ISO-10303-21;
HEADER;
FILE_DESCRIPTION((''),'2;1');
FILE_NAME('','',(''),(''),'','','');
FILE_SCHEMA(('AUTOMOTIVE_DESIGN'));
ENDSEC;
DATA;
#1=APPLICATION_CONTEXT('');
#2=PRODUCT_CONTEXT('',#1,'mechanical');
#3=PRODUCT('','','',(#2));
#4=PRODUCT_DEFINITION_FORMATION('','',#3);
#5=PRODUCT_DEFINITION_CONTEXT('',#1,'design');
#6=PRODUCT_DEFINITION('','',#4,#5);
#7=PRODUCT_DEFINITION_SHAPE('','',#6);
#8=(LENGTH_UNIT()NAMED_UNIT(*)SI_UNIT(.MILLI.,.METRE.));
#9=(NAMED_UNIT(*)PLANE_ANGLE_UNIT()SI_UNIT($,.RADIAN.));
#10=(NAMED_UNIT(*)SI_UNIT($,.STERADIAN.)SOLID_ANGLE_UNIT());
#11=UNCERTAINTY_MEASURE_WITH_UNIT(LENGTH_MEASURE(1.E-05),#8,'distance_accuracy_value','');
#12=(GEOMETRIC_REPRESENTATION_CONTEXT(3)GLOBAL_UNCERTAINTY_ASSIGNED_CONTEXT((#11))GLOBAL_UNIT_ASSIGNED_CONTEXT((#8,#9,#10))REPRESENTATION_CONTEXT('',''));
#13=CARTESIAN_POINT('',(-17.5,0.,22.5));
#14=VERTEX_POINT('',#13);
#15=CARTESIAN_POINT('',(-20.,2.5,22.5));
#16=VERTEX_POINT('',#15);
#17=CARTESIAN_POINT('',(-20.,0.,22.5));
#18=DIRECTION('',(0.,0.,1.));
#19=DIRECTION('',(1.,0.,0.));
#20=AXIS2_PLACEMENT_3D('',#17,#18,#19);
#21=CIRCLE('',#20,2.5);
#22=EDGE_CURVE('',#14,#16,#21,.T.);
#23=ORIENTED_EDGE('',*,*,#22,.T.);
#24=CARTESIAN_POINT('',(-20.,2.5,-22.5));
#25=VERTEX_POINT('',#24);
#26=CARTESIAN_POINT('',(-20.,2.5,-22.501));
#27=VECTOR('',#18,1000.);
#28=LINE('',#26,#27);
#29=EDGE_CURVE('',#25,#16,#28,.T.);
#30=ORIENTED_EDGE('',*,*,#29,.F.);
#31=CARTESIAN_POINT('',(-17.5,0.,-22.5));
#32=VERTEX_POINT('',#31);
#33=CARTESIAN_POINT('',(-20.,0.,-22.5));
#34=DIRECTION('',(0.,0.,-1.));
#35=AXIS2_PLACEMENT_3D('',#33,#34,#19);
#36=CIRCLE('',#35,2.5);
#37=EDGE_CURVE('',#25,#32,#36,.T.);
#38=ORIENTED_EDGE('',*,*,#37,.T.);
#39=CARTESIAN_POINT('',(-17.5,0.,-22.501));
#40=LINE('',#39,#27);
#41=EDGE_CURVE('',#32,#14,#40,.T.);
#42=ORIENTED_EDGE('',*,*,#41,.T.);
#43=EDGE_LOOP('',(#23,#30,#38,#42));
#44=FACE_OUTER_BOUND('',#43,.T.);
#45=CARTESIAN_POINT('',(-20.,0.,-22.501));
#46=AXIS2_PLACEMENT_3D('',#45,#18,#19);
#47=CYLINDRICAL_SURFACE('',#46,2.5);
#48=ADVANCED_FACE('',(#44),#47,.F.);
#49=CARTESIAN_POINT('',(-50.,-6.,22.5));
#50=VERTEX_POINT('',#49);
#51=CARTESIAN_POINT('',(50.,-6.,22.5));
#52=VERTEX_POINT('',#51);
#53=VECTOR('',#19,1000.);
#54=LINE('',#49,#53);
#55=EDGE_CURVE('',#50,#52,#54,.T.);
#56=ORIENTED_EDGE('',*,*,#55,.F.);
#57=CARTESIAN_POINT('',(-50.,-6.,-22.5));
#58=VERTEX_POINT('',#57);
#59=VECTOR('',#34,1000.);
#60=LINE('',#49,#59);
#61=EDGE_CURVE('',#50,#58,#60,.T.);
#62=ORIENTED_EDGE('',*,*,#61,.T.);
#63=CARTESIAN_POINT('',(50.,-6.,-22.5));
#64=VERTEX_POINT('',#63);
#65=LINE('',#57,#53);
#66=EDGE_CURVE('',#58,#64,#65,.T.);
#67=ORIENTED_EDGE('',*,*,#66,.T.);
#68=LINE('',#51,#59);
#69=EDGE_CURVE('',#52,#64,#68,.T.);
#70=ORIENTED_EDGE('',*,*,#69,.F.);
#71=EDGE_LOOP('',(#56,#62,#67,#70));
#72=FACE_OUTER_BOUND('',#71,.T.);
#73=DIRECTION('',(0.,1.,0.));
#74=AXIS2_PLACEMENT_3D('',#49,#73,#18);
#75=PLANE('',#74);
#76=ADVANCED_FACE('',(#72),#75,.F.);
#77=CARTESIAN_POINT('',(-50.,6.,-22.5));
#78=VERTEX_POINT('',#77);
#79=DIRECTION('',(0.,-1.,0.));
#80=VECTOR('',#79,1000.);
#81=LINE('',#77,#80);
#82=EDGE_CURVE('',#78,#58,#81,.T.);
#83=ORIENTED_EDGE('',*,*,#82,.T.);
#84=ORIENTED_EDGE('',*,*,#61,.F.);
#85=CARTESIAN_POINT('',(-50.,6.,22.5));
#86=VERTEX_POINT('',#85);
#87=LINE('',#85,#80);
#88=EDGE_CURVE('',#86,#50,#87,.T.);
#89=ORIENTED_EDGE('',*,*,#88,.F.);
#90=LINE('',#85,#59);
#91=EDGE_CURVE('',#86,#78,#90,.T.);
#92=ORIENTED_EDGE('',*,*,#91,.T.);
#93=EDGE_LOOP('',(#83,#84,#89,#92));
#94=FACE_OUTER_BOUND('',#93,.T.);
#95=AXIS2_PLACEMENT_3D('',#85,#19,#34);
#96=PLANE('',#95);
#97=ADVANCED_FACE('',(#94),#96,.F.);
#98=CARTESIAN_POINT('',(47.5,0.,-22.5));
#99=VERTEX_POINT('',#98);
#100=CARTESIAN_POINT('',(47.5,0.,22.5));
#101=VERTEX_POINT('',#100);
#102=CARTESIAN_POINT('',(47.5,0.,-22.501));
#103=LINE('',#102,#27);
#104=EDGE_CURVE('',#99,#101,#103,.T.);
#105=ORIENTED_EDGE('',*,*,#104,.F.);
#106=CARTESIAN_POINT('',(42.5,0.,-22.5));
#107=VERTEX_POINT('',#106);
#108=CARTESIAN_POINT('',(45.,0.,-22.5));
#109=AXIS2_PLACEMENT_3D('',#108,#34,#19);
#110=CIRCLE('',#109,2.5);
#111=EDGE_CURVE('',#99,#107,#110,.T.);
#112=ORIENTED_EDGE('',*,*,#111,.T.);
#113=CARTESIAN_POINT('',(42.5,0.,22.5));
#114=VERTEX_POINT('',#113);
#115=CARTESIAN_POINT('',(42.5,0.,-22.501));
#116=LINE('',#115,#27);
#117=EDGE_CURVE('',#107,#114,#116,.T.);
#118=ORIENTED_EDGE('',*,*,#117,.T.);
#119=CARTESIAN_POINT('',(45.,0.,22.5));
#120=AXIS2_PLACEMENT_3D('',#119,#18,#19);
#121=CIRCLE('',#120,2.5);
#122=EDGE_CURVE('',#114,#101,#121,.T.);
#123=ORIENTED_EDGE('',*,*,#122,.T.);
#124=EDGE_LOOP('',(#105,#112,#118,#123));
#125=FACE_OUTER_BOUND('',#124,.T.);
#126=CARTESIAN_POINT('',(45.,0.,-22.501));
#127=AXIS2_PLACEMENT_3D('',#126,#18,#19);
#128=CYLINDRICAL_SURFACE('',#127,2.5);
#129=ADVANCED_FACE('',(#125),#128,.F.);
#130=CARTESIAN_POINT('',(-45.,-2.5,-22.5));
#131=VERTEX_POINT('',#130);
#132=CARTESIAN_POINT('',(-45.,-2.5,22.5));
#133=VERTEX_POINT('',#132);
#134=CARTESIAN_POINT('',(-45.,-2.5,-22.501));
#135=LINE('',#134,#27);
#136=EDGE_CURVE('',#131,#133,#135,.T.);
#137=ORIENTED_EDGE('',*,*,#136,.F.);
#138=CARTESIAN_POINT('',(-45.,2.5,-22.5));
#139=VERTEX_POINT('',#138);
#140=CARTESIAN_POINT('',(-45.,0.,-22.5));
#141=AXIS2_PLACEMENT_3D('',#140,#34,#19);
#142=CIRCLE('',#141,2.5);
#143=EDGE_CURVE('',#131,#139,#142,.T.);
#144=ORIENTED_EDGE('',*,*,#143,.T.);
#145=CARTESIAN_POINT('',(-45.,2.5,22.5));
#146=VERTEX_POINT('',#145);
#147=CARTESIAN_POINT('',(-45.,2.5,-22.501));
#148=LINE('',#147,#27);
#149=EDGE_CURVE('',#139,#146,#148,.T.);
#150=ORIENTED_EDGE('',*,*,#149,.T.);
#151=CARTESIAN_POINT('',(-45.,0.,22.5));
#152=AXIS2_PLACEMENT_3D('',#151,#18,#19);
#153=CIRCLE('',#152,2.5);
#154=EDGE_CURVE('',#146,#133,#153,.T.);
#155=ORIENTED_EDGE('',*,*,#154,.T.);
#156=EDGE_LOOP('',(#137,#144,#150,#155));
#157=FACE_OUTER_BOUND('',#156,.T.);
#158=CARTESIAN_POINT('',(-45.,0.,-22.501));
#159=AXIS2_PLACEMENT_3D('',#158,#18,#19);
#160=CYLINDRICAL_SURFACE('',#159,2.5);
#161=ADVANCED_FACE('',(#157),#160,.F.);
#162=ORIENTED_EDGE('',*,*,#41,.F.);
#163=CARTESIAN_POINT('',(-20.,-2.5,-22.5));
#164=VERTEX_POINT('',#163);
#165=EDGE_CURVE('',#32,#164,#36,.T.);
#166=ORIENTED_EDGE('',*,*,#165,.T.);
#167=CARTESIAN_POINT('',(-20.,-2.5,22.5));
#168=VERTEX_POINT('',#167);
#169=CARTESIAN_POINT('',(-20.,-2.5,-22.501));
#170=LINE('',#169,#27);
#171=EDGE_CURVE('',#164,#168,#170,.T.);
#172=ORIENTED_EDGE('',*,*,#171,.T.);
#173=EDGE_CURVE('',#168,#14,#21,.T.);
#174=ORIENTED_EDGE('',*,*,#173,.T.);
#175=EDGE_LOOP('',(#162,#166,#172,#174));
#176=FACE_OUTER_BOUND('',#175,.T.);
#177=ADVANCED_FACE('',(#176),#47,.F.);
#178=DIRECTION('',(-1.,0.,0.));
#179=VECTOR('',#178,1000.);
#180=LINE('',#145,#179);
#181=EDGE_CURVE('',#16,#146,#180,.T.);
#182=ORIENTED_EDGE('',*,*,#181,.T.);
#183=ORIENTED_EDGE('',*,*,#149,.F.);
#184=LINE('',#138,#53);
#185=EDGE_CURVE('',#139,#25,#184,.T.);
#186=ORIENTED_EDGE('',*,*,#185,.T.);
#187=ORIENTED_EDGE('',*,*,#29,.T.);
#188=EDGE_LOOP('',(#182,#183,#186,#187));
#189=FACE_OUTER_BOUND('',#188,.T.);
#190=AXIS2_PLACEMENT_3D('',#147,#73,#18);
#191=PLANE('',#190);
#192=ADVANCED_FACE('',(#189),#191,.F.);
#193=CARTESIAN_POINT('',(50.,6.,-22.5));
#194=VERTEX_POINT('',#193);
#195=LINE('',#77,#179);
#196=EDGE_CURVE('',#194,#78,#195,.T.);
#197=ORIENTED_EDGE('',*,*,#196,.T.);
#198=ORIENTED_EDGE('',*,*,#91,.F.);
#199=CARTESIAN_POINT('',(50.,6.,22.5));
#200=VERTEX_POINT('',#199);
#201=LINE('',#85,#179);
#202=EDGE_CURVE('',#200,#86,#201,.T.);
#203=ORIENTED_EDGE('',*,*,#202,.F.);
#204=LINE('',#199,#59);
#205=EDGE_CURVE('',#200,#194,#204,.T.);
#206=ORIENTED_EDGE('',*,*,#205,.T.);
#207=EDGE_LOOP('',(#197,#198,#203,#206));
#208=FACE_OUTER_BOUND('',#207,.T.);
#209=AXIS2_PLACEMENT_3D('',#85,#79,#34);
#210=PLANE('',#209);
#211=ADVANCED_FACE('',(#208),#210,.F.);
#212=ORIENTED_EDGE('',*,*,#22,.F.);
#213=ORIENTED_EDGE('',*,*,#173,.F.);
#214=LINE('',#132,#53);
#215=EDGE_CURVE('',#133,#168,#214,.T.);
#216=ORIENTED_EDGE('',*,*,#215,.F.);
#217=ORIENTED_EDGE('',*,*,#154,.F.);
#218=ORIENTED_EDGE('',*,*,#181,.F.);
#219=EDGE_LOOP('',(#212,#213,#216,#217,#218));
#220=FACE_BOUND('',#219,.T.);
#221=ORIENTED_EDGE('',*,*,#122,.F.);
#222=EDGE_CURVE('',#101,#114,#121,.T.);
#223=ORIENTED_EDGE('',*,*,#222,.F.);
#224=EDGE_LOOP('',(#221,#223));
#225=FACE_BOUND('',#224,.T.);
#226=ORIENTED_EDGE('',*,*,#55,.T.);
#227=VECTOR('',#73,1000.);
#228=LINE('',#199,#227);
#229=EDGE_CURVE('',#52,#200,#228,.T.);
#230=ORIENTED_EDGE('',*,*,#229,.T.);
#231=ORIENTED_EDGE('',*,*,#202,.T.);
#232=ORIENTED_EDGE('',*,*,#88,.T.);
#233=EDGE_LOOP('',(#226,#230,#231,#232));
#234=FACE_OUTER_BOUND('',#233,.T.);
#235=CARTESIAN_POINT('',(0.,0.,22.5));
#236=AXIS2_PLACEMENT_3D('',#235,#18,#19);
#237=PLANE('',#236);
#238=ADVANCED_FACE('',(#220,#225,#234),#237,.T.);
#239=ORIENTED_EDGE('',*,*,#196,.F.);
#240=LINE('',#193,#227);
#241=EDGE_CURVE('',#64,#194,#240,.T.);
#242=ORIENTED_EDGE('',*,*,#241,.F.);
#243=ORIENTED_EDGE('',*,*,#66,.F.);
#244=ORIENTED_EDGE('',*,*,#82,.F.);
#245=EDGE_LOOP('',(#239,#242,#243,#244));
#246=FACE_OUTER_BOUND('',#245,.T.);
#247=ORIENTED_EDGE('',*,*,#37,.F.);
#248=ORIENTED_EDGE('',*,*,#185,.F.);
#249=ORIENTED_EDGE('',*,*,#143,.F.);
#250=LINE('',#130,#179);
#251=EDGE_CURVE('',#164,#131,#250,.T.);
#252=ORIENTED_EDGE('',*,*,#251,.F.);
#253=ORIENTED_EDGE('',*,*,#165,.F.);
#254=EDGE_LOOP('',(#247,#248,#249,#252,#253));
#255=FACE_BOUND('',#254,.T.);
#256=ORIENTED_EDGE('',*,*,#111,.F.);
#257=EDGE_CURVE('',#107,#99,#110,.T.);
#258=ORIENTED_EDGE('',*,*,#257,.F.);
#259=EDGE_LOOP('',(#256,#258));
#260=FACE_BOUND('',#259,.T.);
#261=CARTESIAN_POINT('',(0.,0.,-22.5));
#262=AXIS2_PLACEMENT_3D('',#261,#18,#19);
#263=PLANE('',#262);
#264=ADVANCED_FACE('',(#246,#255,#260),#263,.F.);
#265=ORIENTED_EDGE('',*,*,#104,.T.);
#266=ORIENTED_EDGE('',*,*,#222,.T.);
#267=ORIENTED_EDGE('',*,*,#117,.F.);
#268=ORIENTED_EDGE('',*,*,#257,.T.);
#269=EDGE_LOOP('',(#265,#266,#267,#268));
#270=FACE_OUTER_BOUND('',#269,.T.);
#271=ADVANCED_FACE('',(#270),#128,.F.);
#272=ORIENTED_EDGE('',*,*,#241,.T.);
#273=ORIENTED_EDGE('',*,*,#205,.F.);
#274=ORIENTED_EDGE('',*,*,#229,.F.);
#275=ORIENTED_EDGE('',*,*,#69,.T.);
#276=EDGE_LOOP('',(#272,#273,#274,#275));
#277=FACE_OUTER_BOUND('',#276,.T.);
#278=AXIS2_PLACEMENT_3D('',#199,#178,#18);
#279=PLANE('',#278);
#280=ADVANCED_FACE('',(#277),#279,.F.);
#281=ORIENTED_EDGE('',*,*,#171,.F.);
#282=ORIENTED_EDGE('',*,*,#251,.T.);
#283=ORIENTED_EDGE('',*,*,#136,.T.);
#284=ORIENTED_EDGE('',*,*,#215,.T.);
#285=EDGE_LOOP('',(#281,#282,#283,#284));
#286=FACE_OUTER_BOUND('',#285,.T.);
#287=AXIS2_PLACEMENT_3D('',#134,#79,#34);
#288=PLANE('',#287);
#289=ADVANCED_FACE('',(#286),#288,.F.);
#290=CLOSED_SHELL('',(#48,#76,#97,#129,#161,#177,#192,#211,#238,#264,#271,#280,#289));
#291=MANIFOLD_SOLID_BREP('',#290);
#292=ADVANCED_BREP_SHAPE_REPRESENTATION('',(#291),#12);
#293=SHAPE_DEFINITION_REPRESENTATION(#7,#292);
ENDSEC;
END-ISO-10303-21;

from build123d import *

# Parameters (mm, degrees)
PLATE_PROFILE_SKETCH_W          = 100
PLATE_PROFILE_SKETCH_H          = 12
BASE_PLATE_100X12X45_DEPTH      = 22.5
THROUGH_SLOT_AND_HOLE_CUT_REACH = 69.535
SLOT_AND_HOLE_SKETCH_R          = 2.5


with BuildPart() as part:
    # Plate Profile Sketch → Base Plate 100x12x45 (new, symmetric)
    with BuildSketch(Plane.XY):
        Rectangle(PLATE_PROFILE_SKETCH_W, PLATE_PROFILE_SKETCH_H)
    extrude(amount=BASE_PLATE_100X12X45_DEPTH, both=True)

    # Slot and Hole Sketch → Through Slot and Hole Cut (cut, up to next)
    with BuildSketch(Plane.XY.offset(22.5), mode=Mode.PRIVATE) as through_slot_and_hole_cut_sk1:
        with Locations((45, 0)):
            Circle(SLOT_AND_HOLE_SKETCH_R)
    through_slot_and_hole_cut_tool1 = extrude(through_slot_and_hole_cut_sk1.sketch, amount=-THROUGH_SLOT_AND_HOLE_CUT_REACH, mode=Mode.PRIVATE) & part.part
    # Slot and Hole Sketch → Through Slot and Hole Cut (cut, up to next)
    with BuildSketch(Plane.XY.offset(22.5), mode=Mode.PRIVATE) as through_slot_and_hole_cut_sk2:
        with BuildLine():
            Line((-45, 2.5), (-20, 2.5))
            ThreePointArc((-20, 2.5), (-17.5, 0), (-20, -2.5))
            Line((-20, -2.5), (-45, -2.5))
            ThreePointArc((-45, -2.5), (-47.5, 0), (-45, 2.5))
        make_face()
    through_slot_and_hole_cut_tool2 = extrude(through_slot_and_hole_cut_sk2.sketch, amount=-THROUGH_SLOT_AND_HOLE_CUT_REACH, mode=Mode.PRIVATE) & part.part
    add(through_slot_and_hole_cut_tool1.solids().sort_by_distance((45, 0, 22.5))[0], mode=Mode.SUBTRACT)
    add(through_slot_and_hole_cut_tool2.solids().sort_by_distance((-32.5, 0, 22.5))[0], mode=Mode.SUBTRACT)


solid = part.part
